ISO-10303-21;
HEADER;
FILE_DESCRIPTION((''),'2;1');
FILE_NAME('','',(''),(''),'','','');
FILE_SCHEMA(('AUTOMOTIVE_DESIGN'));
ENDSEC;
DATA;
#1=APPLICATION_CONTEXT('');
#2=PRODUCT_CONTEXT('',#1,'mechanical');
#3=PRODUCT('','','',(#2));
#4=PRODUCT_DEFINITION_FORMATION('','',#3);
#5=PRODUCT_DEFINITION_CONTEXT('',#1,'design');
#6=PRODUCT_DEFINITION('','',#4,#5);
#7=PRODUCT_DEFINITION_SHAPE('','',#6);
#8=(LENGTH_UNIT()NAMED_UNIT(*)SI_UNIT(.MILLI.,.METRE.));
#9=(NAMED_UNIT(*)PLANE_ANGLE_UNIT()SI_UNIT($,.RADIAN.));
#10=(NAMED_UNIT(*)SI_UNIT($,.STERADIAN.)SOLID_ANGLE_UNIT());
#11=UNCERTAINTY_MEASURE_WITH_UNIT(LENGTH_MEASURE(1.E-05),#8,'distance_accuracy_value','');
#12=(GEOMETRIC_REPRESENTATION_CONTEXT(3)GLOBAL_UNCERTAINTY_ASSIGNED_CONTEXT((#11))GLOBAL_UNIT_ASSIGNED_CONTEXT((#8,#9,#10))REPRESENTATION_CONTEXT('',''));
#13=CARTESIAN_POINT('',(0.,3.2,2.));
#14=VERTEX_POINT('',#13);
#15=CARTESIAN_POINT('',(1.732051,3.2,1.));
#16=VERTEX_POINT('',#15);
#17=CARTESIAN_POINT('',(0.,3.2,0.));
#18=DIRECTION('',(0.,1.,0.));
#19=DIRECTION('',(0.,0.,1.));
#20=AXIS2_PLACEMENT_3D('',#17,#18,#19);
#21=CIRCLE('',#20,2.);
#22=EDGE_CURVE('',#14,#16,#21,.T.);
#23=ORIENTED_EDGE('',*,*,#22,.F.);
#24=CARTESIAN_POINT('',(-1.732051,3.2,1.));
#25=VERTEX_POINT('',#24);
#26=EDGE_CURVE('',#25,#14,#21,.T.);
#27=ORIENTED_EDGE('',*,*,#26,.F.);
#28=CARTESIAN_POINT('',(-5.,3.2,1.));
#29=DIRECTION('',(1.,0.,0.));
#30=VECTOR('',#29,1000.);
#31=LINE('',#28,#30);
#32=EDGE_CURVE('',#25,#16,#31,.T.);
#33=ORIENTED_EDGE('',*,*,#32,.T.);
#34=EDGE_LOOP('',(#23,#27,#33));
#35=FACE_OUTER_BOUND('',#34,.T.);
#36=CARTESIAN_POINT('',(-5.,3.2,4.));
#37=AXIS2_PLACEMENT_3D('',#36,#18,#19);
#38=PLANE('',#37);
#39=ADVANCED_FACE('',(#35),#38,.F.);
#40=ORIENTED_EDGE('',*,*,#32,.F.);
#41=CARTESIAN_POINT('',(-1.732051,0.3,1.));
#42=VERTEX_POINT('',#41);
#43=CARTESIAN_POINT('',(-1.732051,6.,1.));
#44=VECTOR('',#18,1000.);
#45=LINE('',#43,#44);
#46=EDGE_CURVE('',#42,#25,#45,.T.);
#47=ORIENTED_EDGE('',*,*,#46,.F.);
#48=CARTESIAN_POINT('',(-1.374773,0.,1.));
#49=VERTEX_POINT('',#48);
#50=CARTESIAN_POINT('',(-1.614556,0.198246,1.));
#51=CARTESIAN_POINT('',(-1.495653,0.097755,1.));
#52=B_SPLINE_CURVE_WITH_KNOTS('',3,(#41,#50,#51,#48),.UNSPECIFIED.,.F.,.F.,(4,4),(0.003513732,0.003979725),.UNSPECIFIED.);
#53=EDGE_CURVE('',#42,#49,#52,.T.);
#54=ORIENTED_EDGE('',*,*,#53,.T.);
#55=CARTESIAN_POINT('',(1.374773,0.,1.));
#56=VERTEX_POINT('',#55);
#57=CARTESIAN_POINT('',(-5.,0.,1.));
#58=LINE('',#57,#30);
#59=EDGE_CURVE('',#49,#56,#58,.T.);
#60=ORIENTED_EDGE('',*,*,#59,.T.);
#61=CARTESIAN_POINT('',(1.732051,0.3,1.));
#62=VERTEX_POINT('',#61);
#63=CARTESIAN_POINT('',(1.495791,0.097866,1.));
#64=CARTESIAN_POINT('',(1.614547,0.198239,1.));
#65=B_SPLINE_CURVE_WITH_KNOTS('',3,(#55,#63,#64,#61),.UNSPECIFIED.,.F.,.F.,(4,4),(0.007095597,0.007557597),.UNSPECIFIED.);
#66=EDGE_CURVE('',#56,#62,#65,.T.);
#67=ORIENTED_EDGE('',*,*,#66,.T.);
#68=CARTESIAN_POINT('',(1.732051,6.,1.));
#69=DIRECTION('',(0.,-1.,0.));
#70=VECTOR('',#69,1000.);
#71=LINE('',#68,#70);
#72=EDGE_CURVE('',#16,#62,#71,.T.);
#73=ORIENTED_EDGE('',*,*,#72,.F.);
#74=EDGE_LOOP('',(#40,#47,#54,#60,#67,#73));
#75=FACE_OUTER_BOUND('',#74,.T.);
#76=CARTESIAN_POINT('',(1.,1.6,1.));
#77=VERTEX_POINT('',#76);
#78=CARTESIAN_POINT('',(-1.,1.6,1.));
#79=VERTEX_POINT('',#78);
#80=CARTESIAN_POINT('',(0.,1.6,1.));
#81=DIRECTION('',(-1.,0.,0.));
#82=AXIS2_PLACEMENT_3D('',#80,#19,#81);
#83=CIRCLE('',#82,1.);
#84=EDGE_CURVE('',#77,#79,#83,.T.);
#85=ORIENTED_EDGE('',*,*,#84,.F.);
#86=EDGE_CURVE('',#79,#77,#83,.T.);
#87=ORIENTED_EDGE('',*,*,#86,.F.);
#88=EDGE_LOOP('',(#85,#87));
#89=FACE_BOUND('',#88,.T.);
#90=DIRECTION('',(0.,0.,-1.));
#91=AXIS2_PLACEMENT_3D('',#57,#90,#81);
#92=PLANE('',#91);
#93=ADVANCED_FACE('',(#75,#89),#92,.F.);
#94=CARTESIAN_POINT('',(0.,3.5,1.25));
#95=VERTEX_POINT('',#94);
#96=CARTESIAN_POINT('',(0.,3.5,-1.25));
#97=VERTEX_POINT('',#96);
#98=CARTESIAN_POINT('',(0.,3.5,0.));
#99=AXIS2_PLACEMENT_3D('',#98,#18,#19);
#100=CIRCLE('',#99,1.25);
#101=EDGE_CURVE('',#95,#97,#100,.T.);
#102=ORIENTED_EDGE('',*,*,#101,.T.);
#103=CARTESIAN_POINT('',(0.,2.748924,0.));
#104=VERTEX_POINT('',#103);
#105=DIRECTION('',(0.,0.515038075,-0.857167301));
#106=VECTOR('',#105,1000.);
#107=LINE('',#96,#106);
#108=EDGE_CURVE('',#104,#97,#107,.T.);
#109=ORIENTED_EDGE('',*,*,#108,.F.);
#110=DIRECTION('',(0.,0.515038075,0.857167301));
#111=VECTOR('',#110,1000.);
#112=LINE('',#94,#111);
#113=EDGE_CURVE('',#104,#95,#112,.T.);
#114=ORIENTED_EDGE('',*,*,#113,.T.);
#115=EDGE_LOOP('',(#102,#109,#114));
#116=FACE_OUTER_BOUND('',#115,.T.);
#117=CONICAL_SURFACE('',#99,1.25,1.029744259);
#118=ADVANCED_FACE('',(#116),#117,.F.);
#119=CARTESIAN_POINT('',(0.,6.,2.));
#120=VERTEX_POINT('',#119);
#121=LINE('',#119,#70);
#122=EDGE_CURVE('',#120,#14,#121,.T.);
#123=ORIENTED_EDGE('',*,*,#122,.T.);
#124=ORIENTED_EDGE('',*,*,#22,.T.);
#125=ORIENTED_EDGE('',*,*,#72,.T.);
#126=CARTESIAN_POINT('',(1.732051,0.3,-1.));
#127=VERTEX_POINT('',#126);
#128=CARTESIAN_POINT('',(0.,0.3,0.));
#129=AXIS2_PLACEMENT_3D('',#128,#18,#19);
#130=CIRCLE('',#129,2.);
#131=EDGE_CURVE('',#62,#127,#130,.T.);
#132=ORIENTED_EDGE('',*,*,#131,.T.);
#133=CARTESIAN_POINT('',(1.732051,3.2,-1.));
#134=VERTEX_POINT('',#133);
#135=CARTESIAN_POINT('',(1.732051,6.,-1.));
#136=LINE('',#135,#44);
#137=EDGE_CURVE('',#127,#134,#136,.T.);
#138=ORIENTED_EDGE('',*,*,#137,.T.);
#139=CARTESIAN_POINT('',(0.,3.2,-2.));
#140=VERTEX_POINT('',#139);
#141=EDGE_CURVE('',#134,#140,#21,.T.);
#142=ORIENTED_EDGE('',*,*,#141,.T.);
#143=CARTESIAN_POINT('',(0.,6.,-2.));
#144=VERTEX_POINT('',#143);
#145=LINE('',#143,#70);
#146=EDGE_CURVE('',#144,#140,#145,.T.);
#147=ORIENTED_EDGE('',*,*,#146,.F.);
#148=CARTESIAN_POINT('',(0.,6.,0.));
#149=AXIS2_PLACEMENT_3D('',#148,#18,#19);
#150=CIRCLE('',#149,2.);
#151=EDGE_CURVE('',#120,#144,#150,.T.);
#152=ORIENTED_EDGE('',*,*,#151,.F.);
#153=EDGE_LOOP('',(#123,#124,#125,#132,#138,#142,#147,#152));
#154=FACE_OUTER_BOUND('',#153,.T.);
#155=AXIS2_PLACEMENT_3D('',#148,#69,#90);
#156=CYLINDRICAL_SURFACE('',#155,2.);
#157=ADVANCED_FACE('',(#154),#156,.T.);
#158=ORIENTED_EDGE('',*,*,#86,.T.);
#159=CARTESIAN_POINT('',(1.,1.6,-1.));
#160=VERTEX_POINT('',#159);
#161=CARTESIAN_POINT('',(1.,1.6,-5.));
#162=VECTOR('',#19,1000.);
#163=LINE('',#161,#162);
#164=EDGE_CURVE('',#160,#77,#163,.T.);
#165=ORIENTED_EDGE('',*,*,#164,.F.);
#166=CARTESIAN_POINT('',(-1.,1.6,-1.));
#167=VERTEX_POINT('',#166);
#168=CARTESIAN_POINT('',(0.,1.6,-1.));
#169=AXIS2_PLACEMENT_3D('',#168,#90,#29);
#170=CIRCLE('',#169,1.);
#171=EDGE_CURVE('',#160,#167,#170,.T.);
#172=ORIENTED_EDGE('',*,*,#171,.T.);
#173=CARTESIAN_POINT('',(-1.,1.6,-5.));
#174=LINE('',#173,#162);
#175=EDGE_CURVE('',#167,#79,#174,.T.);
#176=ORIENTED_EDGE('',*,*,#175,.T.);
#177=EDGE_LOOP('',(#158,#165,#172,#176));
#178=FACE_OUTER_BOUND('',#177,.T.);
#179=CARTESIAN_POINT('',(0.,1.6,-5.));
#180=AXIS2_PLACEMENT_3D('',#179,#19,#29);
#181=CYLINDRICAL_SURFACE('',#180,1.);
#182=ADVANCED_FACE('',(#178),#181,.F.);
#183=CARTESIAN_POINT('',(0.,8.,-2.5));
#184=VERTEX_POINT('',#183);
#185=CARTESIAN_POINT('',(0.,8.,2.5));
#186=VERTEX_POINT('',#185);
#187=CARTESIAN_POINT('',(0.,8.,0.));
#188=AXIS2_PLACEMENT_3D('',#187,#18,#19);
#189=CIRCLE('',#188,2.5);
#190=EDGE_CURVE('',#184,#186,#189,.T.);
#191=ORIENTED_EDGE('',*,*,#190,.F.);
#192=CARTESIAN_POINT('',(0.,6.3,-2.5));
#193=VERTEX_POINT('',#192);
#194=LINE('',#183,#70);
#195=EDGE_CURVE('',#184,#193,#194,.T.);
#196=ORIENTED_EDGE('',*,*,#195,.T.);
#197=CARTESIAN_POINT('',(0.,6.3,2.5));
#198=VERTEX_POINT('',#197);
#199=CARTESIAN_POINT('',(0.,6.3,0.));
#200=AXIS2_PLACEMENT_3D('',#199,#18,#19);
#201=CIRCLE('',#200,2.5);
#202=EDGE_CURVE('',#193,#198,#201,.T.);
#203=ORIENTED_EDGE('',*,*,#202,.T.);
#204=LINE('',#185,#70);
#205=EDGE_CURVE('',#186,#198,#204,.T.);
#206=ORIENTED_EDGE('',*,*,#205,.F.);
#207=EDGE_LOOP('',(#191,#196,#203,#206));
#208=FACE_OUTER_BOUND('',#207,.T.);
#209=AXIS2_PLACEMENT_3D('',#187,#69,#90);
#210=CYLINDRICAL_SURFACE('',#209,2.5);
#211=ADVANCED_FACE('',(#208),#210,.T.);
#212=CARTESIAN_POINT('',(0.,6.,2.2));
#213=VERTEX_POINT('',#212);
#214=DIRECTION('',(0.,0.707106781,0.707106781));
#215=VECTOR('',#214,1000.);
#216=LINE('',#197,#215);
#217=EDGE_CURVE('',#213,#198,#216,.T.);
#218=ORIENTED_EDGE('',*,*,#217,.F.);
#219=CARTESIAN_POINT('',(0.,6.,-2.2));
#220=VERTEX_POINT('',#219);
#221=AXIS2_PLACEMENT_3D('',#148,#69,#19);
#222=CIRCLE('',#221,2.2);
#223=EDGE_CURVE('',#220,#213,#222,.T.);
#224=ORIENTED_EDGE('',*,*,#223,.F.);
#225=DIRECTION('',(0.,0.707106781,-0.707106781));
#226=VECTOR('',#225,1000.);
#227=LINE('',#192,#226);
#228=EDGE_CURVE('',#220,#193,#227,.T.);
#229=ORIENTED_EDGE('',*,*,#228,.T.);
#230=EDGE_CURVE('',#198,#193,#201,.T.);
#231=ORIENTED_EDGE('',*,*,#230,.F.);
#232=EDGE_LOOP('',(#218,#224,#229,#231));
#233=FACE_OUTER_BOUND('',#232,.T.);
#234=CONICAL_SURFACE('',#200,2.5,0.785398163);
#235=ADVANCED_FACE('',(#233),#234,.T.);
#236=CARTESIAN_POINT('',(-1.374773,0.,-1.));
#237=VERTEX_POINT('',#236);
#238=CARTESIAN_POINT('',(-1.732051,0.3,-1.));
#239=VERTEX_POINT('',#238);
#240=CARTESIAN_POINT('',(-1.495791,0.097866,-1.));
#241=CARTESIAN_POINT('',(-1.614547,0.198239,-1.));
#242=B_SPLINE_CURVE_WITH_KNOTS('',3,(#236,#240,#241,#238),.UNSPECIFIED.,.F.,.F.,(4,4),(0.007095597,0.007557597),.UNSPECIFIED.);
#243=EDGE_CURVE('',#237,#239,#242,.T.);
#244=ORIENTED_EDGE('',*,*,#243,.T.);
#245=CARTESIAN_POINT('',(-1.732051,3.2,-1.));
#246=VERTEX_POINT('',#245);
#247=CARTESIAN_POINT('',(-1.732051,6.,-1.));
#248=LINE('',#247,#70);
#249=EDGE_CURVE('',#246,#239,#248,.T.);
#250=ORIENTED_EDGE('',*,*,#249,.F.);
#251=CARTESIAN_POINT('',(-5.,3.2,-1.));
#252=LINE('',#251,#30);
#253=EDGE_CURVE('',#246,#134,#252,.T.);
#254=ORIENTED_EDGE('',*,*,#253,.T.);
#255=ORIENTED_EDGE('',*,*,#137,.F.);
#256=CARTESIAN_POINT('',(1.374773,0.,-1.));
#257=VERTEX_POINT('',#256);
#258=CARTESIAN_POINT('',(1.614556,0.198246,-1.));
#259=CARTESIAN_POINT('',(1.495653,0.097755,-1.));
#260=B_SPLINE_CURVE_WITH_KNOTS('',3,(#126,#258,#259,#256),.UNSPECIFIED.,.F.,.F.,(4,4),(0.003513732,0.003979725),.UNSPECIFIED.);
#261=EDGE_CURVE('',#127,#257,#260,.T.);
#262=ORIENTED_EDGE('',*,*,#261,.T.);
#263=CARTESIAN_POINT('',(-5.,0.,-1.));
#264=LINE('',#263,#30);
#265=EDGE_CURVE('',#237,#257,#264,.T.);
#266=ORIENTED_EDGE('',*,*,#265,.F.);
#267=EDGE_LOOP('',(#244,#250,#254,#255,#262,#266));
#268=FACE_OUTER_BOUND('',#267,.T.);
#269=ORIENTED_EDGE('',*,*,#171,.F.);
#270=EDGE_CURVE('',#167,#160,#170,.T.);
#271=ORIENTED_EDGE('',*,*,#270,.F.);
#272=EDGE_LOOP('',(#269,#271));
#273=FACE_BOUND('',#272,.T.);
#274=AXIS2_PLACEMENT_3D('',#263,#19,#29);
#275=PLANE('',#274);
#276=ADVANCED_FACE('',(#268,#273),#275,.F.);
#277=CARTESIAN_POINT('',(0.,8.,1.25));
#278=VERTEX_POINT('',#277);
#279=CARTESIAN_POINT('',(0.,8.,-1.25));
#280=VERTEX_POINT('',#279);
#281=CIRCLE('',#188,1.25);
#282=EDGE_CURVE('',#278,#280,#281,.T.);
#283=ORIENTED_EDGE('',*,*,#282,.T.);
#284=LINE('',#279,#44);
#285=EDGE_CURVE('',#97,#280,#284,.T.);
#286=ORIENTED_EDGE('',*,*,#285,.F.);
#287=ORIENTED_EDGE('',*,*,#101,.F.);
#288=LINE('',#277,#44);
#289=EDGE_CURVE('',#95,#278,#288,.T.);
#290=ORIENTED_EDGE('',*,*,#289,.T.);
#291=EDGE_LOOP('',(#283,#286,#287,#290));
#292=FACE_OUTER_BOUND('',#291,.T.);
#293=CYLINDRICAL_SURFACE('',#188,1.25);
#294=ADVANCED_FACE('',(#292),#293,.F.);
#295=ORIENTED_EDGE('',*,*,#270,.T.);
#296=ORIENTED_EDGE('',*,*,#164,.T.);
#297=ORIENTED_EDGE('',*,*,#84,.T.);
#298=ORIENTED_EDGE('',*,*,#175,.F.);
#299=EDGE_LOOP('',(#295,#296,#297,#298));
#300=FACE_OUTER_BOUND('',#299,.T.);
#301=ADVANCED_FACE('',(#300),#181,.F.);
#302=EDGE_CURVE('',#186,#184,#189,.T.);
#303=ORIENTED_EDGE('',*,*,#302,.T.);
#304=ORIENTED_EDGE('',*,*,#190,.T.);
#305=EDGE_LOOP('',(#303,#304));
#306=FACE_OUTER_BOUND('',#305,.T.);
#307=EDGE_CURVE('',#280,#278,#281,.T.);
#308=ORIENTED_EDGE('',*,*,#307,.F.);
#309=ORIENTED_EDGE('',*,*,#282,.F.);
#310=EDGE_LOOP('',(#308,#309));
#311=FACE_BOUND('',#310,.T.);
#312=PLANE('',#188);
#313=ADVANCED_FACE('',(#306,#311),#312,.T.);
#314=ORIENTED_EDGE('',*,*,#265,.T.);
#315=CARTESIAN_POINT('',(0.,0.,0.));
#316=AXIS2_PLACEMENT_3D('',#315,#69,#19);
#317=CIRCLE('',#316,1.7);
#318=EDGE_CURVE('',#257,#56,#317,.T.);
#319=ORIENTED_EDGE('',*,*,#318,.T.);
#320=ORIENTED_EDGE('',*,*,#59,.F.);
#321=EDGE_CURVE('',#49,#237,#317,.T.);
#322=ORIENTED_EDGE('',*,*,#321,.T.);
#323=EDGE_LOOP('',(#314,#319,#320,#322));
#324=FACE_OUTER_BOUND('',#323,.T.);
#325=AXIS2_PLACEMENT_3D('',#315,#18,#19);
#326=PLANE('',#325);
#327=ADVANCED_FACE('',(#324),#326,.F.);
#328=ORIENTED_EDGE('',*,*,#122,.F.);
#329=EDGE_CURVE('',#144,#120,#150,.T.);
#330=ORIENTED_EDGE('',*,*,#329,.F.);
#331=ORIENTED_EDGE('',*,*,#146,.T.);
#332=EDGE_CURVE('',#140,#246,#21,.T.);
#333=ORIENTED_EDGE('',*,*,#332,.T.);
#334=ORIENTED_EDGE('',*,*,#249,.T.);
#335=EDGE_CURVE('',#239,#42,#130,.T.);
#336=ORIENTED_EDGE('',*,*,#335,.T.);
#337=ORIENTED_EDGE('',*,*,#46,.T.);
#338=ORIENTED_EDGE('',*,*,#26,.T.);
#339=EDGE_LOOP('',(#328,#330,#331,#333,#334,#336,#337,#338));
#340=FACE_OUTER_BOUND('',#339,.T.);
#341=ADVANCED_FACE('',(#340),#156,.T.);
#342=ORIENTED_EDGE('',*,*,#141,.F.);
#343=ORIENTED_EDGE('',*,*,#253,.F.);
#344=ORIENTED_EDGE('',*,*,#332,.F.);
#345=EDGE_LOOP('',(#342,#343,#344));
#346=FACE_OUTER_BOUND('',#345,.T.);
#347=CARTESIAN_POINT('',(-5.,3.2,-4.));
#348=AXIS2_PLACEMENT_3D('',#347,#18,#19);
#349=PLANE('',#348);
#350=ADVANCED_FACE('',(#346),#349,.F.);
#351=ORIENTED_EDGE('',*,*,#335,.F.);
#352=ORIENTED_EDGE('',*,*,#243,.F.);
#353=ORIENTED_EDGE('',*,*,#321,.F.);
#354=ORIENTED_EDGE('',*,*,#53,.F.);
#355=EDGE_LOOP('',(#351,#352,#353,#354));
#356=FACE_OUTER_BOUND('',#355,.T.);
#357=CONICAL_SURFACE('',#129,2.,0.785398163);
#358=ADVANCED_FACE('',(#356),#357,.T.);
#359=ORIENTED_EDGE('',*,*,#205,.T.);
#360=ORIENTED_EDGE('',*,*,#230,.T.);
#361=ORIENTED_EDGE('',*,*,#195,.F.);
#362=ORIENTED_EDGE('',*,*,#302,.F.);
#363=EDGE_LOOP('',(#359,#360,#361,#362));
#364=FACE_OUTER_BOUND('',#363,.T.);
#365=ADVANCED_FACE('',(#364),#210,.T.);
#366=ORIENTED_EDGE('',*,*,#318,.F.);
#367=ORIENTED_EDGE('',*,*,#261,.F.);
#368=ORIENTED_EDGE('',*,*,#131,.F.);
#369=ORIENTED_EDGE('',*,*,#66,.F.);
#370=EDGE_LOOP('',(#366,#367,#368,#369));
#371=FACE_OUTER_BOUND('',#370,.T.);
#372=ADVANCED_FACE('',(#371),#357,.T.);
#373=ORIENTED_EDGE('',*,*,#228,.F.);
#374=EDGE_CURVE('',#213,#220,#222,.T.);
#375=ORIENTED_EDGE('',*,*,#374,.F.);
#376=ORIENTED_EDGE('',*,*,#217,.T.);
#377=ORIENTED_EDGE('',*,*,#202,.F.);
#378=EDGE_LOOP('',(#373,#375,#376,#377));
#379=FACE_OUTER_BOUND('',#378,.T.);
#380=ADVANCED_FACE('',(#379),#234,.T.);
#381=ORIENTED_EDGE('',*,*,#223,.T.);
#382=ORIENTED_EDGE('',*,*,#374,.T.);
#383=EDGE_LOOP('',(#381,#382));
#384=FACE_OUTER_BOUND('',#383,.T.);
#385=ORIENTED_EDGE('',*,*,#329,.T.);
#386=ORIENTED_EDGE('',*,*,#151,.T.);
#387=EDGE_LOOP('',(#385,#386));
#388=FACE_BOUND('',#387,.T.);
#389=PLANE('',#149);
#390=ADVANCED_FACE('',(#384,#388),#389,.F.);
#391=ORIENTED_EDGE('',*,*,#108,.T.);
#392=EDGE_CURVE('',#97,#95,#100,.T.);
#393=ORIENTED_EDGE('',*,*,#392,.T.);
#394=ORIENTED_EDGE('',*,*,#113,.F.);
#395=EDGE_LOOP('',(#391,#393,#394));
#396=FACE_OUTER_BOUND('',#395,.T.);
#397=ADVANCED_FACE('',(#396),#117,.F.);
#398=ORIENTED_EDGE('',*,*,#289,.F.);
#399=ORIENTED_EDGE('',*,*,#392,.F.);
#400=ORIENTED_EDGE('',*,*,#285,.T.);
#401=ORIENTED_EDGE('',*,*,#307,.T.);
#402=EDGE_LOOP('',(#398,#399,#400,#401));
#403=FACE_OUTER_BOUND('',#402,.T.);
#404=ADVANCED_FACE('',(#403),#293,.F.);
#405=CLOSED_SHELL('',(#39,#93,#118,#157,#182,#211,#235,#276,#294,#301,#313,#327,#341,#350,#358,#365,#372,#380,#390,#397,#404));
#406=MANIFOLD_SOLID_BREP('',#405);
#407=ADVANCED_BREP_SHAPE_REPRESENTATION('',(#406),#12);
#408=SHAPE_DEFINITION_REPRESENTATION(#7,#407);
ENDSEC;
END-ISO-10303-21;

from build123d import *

# Parameters (mm, degrees)
SKETCH1_R             = 2
BOSS_EXTRUDE1_DEPTH   = 6
SKETCH2_R             = 2.5
BOSS_EXTRUDE2_DEPTH   = 2
M3_TAPPED_HOLE1_D     = 2.5
M3_TAPPED_HOLE1_DEPTH = 4.5
M3_TAPPED_HOLE1_TIP   = 0.751075774
CHAMFER1_SIZE         = 0.3
SKETCH6_R             = 1
CUT_EXTRUDE1_DEPTH    = 5
SKETCH7_W             = 3
SKETCH7_H             = 3.2
CUT_EXTRUDE2_DEPTH    = 5


with BuildPart() as part:
    # Sketch1 → Boss-Extrude1 (new body)
    with BuildSketch(Plane(origin=(0, 0, 0), x_dir=(1, 0, 0), z_dir=(0, 1, 0))):
        with Locations(Location((0, 0, 0), (0, 0, 270))):
            Circle(SKETCH1_R)
    extrude(amount=BOSS_EXTRUDE1_DEPTH)

    # Sketch2 → Boss-Extrude2 (add)
    with BuildSketch(Plane(origin=(0, 6, 0), x_dir=(1, 0, 0), z_dir=(0, 1, 0))):
        with Locations(Location((0, 0, 0), (0, 0, 270))):
            Circle(SKETCH2_R)
    extrude(amount=BOSS_EXTRUDE2_DEPTH)

    # M3 Tapped Hole1
    with Locations(Plane(origin=(0, 8, 0), x_dir=(1, 0, 0), z_dir=(0, 1, 0))):
        with Locations((0, 0)):
            Hole(M3_TAPPED_HOLE1_D / 2, depth=M3_TAPPED_HOLE1_DEPTH)
            with Locations((0, 0, -(M3_TAPPED_HOLE1_DEPTH + M3_TAPPED_HOLE1_TIP / 2))):  # 118° drill point
                Cone(0, M3_TAPPED_HOLE1_D / 2, M3_TAPPED_HOLE1_TIP, mode=Mode.SUBTRACT)

    # Chamfer1
    chamfer1_edges = [part.edges().sort_by_distance(p)[0] for p in [
        (0, 0, -2),
        (0, 6, -2.5),
    ]]
    chamfer(chamfer1_edges, length=CHAMFER1_SIZE)

    # Sketch6 → Cut-Extrude1 (cut, symmetric)
    with BuildSketch(Plane.XY):
        with Locations(Location((0, 1.6, 0), (0, 0, 90.00000001))):
            Circle(SKETCH6_R)
    extrude(amount=CUT_EXTRUDE1_DEPTH, both=True, mode=Mode.SUBTRACT)

    # Sketch7 → Cut-Extrude2 (cut, symmetric)
    with BuildSketch(Plane(origin=(0, 0, 0), x_dir=(0, 0, -1), z_dir=(1, 0, 0))):
        with Locations((2.5, 1.6)):
            Rectangle(SKETCH7_W, SKETCH7_H)
        with Locations((-2.5, 1.6)):
            Rectangle(SKETCH7_W, SKETCH7_H)
    extrude(amount=CUT_EXTRUDE2_DEPTH, both=True, mode=Mode.SUBTRACT)


solid = part.part
